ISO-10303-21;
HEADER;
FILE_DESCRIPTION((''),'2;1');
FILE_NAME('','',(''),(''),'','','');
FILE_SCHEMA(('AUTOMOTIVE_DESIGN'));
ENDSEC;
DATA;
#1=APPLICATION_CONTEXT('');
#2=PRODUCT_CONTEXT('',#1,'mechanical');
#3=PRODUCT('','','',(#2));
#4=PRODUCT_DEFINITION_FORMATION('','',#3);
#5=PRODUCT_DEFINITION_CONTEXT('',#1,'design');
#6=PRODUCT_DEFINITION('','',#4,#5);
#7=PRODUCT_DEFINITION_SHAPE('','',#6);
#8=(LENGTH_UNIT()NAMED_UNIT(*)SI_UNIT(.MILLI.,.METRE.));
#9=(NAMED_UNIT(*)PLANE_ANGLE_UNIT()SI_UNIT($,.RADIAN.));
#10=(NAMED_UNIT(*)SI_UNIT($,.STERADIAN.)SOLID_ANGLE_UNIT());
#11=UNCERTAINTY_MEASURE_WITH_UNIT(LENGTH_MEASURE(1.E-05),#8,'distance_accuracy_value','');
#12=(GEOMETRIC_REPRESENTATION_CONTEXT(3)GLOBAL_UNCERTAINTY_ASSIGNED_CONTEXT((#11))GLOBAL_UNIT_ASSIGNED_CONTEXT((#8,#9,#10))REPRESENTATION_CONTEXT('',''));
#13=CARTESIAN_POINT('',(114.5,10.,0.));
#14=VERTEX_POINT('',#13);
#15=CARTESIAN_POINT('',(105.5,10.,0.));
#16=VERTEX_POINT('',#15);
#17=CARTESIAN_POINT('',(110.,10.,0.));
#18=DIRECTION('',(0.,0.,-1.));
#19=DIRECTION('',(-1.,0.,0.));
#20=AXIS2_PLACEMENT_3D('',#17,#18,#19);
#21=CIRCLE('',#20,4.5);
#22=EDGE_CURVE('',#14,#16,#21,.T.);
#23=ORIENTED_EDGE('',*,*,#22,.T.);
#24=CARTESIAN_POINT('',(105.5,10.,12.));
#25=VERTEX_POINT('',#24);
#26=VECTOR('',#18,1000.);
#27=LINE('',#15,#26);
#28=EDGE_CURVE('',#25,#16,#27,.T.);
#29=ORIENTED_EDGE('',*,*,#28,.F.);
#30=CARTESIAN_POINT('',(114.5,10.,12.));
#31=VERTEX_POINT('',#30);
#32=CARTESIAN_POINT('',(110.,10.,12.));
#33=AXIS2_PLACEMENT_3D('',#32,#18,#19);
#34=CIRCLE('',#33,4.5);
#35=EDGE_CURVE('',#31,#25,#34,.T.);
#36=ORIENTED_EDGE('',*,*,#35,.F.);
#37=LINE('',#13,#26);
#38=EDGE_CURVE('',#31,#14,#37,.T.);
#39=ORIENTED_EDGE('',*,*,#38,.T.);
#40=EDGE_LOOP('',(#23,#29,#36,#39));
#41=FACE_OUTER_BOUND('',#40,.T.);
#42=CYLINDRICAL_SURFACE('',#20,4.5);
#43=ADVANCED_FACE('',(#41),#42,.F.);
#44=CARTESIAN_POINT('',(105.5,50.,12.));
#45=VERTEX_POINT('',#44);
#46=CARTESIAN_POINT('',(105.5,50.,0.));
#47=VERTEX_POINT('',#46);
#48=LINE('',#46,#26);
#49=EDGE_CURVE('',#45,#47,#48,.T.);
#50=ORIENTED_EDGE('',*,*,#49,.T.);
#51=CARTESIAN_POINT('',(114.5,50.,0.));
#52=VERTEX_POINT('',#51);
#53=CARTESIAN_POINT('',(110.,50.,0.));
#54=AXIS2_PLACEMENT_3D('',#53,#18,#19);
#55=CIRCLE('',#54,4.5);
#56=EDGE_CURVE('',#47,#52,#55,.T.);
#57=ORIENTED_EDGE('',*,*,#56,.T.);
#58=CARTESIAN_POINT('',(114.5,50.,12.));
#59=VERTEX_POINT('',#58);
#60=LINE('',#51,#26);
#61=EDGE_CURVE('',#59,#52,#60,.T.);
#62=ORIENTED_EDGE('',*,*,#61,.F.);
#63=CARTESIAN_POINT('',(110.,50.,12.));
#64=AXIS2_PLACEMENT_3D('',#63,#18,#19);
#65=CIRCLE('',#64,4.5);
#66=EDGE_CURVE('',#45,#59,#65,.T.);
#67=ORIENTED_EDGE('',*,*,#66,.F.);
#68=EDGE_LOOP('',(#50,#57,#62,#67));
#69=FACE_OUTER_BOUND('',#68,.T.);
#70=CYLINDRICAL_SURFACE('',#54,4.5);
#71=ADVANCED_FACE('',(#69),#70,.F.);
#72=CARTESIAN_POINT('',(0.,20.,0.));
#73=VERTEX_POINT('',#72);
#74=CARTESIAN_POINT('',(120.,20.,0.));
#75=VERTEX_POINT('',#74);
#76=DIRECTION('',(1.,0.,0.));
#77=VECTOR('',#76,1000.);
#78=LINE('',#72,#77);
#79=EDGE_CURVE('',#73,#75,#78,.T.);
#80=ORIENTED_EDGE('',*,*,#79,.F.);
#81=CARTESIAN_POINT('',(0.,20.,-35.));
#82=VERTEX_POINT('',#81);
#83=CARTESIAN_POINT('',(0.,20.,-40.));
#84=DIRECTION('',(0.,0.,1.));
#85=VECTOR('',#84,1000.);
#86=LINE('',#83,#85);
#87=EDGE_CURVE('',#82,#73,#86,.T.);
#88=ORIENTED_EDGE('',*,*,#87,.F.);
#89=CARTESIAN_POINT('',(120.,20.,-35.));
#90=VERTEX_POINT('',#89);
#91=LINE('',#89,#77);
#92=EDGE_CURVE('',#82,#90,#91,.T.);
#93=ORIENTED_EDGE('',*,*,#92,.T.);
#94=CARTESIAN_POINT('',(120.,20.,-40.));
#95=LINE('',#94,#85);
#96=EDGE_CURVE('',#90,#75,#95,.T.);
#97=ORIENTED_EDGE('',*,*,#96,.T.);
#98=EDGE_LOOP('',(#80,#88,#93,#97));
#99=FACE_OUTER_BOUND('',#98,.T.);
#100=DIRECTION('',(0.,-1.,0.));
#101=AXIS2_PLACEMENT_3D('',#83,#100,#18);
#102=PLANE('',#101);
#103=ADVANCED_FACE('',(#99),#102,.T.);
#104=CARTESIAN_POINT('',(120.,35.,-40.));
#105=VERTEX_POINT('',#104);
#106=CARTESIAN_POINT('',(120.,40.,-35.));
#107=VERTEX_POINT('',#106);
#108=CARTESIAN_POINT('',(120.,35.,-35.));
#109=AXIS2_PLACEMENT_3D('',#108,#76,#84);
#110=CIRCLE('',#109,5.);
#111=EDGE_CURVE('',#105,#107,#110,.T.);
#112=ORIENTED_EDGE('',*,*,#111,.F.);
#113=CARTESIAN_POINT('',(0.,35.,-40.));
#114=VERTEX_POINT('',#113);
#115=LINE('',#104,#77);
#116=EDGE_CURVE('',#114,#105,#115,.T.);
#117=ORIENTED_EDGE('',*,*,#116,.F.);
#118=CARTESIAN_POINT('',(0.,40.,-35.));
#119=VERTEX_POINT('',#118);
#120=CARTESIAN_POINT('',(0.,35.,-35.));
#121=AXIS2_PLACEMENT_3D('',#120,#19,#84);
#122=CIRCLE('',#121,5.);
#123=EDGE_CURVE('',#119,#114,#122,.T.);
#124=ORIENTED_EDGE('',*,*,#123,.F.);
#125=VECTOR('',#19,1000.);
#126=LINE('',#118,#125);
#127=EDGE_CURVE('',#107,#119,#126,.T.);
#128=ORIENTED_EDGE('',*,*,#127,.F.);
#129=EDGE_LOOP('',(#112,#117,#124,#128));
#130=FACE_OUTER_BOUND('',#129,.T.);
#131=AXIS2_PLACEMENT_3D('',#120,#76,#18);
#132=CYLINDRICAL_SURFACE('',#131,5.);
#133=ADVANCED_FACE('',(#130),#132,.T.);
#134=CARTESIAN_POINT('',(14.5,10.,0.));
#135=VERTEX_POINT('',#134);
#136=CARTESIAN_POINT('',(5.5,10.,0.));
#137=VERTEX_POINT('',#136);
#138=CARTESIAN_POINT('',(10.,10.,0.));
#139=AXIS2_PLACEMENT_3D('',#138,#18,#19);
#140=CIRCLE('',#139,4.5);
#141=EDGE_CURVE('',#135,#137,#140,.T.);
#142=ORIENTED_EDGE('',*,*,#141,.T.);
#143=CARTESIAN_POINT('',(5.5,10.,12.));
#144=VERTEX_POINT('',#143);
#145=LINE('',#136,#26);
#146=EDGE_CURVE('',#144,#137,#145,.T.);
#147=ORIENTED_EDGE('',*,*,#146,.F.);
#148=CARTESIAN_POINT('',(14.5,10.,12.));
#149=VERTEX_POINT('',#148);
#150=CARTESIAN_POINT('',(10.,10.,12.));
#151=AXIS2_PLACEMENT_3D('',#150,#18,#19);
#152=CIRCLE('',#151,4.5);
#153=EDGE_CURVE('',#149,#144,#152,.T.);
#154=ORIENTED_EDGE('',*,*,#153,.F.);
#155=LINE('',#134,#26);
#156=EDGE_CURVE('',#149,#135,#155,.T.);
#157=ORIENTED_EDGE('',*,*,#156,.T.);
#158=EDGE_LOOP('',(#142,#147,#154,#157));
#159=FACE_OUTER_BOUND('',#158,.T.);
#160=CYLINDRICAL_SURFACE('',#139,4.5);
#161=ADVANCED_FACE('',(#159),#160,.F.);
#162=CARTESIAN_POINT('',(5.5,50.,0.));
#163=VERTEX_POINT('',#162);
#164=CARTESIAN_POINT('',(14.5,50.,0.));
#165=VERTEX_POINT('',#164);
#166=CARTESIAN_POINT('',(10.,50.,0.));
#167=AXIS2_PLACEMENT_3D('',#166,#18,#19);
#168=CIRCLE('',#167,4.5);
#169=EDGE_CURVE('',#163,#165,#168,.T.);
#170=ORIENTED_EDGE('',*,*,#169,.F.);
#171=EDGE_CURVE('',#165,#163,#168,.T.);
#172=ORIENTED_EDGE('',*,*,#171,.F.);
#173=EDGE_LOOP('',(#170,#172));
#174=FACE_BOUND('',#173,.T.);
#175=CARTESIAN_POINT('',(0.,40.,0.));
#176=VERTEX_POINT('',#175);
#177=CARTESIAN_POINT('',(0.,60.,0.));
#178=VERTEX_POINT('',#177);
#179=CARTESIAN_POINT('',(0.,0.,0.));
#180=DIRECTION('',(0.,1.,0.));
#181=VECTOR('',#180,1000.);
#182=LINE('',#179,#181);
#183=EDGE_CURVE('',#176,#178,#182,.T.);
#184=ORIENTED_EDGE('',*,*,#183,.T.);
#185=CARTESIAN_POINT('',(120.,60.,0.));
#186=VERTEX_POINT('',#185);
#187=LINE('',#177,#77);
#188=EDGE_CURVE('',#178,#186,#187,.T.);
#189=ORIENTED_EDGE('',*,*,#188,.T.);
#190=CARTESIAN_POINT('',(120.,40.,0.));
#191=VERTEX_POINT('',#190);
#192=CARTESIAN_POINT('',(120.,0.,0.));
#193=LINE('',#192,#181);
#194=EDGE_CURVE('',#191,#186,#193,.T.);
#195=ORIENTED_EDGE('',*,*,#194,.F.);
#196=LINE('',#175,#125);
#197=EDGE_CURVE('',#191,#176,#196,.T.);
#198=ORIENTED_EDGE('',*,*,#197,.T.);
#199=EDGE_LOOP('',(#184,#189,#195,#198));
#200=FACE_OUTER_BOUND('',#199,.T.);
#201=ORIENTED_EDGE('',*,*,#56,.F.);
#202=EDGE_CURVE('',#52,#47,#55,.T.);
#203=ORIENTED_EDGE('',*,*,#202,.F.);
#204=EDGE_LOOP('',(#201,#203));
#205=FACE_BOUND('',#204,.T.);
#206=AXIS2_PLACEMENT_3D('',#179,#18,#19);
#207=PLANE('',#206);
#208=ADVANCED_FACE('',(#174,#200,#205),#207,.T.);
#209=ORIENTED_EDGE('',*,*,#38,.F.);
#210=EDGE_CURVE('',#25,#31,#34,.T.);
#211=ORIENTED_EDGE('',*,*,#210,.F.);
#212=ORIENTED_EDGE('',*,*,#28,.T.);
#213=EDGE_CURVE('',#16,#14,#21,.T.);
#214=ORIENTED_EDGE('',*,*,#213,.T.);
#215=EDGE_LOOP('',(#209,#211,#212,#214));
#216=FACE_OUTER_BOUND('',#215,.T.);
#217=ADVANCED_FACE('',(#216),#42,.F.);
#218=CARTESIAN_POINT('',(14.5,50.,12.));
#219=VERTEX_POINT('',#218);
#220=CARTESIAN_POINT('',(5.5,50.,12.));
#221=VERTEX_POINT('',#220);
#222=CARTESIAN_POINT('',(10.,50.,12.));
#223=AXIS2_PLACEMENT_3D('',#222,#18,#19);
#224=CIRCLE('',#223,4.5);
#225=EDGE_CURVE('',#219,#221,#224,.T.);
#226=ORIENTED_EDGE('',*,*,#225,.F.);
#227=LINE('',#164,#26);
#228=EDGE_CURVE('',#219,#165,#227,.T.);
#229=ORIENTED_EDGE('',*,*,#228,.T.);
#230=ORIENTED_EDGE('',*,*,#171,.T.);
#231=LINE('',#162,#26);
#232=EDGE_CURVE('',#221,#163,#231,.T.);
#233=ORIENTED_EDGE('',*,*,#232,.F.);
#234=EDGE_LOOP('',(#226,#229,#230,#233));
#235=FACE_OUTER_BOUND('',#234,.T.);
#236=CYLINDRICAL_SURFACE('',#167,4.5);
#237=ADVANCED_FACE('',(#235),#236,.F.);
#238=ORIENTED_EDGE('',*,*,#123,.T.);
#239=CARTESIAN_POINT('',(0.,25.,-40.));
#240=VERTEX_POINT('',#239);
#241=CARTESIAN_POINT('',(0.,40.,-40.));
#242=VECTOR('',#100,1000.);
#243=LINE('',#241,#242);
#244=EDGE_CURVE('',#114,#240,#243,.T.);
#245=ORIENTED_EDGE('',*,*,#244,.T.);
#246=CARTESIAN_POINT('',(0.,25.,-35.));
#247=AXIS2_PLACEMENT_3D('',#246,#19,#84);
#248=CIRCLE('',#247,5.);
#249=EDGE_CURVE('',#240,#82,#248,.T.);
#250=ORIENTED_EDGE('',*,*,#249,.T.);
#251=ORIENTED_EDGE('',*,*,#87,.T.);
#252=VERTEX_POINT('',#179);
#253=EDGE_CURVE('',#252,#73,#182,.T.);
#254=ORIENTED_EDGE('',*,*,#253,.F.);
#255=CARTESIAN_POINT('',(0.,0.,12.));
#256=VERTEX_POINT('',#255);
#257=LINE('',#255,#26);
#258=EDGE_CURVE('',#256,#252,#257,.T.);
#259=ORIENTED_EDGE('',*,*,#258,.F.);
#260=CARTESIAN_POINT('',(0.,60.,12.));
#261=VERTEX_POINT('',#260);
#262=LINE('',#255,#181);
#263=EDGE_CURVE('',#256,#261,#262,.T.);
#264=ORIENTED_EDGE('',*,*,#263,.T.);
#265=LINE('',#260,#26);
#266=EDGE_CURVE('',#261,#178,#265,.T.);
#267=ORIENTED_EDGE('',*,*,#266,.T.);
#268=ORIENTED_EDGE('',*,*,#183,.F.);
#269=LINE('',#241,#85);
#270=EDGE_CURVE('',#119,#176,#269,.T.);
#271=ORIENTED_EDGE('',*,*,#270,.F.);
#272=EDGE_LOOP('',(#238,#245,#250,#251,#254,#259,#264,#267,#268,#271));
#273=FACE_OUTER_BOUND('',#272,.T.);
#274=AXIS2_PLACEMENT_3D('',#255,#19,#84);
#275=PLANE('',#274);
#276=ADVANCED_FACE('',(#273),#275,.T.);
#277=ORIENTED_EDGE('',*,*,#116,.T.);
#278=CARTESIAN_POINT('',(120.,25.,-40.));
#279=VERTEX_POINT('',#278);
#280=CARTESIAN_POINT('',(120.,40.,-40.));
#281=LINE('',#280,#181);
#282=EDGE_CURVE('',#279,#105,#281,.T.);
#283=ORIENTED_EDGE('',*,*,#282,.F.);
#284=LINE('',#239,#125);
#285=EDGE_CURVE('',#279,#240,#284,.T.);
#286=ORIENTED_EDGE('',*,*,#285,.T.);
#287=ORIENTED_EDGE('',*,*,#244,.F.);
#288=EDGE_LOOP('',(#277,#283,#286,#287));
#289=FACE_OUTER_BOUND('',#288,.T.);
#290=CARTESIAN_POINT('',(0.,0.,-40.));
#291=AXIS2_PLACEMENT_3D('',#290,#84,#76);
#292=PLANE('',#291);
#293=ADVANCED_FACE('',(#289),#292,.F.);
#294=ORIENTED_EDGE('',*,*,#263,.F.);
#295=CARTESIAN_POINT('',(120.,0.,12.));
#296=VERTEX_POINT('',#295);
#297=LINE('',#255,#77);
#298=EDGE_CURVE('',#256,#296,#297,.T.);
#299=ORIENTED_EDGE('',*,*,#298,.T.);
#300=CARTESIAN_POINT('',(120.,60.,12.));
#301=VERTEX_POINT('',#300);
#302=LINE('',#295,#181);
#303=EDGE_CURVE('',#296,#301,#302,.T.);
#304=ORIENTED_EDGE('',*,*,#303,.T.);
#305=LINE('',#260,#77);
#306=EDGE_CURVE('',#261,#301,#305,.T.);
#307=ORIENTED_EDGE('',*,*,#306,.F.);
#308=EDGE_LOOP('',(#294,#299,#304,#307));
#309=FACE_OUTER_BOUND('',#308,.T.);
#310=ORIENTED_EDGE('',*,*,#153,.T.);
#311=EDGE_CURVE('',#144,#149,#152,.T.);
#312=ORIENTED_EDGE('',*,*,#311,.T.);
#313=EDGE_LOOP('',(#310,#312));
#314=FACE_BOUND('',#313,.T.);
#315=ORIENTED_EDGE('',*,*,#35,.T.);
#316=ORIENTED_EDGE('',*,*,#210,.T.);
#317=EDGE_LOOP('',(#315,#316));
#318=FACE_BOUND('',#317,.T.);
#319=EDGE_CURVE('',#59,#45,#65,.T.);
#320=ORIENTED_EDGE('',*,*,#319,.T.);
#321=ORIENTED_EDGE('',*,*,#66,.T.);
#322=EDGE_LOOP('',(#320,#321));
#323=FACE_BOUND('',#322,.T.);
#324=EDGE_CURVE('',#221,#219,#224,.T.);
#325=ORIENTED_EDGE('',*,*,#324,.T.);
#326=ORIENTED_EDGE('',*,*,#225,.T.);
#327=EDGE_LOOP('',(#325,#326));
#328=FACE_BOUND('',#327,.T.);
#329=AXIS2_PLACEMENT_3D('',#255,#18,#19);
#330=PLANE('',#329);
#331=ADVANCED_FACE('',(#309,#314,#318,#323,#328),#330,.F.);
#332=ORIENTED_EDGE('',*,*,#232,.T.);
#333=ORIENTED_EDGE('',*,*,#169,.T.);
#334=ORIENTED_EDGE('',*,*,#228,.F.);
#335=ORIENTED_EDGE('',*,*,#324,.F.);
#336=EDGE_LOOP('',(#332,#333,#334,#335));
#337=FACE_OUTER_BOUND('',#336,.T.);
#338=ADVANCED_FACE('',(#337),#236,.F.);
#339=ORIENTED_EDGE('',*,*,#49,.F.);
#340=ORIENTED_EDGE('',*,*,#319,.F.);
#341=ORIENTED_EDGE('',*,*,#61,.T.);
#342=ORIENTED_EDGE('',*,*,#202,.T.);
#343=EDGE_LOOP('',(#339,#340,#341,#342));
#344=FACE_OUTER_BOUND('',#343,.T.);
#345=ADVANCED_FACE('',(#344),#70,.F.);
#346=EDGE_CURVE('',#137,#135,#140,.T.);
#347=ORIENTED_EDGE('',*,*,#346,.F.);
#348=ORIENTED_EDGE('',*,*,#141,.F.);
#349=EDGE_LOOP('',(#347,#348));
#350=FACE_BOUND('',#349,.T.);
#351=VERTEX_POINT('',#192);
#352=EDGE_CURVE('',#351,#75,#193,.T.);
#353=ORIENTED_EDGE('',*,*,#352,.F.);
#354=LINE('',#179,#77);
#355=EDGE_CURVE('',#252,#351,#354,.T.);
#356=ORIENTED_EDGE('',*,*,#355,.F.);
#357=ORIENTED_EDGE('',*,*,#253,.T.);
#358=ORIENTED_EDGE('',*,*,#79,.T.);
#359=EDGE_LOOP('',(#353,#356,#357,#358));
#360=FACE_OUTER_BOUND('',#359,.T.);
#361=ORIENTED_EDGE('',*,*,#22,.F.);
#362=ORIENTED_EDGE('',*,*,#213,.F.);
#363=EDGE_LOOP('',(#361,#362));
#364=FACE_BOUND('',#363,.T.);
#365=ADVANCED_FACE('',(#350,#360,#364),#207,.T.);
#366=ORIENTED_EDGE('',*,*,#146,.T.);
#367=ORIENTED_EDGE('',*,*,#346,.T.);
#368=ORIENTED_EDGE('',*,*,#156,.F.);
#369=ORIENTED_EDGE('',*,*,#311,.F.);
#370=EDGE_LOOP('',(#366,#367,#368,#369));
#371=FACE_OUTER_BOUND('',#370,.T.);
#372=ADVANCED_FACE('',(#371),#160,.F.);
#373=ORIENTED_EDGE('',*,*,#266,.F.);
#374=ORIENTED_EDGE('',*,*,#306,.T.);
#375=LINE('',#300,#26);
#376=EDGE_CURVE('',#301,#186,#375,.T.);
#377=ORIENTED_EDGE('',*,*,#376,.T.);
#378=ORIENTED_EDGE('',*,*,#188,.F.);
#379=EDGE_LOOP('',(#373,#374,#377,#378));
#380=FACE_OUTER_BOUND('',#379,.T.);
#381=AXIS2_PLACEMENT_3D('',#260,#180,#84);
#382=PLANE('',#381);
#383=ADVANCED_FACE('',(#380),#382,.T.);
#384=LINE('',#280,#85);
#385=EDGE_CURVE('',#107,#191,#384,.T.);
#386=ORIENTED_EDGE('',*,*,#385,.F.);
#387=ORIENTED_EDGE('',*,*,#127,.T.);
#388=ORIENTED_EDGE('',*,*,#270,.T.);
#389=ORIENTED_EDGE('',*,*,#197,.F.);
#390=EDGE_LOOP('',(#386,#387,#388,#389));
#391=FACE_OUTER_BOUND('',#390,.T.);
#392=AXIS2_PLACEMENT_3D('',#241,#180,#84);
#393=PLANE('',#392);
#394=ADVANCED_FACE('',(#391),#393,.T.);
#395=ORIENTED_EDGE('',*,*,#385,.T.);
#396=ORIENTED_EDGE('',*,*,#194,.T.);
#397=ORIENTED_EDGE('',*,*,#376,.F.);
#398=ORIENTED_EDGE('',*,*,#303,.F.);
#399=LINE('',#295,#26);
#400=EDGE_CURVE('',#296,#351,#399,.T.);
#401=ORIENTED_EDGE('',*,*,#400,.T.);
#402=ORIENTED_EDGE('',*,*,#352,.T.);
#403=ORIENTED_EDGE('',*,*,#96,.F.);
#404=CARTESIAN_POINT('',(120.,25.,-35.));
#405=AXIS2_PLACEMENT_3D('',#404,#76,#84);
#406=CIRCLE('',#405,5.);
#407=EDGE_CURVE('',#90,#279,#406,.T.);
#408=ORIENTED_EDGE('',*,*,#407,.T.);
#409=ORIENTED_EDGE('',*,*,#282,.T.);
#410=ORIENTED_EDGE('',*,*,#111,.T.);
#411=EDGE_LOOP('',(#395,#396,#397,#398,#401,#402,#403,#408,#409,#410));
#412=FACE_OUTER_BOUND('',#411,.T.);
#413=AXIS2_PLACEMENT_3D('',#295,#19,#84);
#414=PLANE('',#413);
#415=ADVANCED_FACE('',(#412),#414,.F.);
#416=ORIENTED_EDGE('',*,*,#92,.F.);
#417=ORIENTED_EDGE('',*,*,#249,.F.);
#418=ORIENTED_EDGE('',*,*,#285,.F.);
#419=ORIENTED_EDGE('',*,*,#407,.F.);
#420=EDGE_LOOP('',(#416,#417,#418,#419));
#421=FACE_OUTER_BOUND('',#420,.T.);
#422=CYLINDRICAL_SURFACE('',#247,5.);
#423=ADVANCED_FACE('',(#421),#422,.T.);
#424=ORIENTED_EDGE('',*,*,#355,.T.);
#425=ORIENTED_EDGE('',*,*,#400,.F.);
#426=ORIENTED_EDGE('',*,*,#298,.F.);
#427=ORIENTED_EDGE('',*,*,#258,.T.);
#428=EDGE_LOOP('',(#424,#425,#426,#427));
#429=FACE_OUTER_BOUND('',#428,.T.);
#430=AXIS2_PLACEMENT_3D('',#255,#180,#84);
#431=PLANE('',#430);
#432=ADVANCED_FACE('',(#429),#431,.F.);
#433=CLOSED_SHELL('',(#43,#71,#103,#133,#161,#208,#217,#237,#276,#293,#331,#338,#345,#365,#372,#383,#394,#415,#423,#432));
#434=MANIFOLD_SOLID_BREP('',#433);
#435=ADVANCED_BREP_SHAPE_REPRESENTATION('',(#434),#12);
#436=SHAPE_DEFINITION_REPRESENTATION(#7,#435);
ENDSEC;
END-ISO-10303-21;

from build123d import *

# Parameters (mm, degrees)
SKETCH1_W                = 120
SKETCH1_H                = 60
BOSS_EXTRUDE1_DEPTH      = 12
M6_CLEARANCE_HOLE1_D     = 9
M6_CLEARANCE_HOLE1_DEPTH = 32.75
M6_CLEARANCE_HOLE1_TIP   = 2.703872786
SKETCH3_W                = 120
SKETCH3_H                = 20
BOSS_EXTRUDE2_DEPTH      = 40
FILLET1_R                = 5


with BuildPart() as part:
    # Sketch1 → Boss-Extrude1 (new body)
    with BuildSketch(Plane.XY):
        with Locations((60, 30)):
            Rectangle(SKETCH1_W, SKETCH1_H)
    extrude(amount=BOSS_EXTRUDE1_DEPTH)

    # M6 Clearance Hole1
    with Locations(Plane(origin=(0, 0, 0), x_dir=(-1, 0, 0), z_dir=(0, 0, -1))):
        with Locations((-110, 50), (-10, 50), (-10, 10), (-110, 10)):
            Hole(M6_CLEARANCE_HOLE1_D / 2, depth=M6_CLEARANCE_HOLE1_DEPTH)
            with Locations((0, 0, -(M6_CLEARANCE_HOLE1_DEPTH + M6_CLEARANCE_HOLE1_TIP / 2))):  # 118° drill point
                Cone(0, M6_CLEARANCE_HOLE1_D / 2, M6_CLEARANCE_HOLE1_TIP, mode=Mode.SUBTRACT)

    # Sketch3 → Boss-Extrude2 (add)
    with BuildSketch(Plane.XY):
        with Locations((60, 30)):
            Rectangle(SKETCH3_W, SKETCH3_H)
    extrude(amount=-BOSS_EXTRUDE2_DEPTH)

    # Fillet1
    fillet1_edges = [part.edges().sort_by_distance(p)[0] for p in [
        (60, 20, -40),
        (60, 40, -40),
    ]]
    fillet(fillet1_edges, radius=FILLET1_R)


solid = part.part
